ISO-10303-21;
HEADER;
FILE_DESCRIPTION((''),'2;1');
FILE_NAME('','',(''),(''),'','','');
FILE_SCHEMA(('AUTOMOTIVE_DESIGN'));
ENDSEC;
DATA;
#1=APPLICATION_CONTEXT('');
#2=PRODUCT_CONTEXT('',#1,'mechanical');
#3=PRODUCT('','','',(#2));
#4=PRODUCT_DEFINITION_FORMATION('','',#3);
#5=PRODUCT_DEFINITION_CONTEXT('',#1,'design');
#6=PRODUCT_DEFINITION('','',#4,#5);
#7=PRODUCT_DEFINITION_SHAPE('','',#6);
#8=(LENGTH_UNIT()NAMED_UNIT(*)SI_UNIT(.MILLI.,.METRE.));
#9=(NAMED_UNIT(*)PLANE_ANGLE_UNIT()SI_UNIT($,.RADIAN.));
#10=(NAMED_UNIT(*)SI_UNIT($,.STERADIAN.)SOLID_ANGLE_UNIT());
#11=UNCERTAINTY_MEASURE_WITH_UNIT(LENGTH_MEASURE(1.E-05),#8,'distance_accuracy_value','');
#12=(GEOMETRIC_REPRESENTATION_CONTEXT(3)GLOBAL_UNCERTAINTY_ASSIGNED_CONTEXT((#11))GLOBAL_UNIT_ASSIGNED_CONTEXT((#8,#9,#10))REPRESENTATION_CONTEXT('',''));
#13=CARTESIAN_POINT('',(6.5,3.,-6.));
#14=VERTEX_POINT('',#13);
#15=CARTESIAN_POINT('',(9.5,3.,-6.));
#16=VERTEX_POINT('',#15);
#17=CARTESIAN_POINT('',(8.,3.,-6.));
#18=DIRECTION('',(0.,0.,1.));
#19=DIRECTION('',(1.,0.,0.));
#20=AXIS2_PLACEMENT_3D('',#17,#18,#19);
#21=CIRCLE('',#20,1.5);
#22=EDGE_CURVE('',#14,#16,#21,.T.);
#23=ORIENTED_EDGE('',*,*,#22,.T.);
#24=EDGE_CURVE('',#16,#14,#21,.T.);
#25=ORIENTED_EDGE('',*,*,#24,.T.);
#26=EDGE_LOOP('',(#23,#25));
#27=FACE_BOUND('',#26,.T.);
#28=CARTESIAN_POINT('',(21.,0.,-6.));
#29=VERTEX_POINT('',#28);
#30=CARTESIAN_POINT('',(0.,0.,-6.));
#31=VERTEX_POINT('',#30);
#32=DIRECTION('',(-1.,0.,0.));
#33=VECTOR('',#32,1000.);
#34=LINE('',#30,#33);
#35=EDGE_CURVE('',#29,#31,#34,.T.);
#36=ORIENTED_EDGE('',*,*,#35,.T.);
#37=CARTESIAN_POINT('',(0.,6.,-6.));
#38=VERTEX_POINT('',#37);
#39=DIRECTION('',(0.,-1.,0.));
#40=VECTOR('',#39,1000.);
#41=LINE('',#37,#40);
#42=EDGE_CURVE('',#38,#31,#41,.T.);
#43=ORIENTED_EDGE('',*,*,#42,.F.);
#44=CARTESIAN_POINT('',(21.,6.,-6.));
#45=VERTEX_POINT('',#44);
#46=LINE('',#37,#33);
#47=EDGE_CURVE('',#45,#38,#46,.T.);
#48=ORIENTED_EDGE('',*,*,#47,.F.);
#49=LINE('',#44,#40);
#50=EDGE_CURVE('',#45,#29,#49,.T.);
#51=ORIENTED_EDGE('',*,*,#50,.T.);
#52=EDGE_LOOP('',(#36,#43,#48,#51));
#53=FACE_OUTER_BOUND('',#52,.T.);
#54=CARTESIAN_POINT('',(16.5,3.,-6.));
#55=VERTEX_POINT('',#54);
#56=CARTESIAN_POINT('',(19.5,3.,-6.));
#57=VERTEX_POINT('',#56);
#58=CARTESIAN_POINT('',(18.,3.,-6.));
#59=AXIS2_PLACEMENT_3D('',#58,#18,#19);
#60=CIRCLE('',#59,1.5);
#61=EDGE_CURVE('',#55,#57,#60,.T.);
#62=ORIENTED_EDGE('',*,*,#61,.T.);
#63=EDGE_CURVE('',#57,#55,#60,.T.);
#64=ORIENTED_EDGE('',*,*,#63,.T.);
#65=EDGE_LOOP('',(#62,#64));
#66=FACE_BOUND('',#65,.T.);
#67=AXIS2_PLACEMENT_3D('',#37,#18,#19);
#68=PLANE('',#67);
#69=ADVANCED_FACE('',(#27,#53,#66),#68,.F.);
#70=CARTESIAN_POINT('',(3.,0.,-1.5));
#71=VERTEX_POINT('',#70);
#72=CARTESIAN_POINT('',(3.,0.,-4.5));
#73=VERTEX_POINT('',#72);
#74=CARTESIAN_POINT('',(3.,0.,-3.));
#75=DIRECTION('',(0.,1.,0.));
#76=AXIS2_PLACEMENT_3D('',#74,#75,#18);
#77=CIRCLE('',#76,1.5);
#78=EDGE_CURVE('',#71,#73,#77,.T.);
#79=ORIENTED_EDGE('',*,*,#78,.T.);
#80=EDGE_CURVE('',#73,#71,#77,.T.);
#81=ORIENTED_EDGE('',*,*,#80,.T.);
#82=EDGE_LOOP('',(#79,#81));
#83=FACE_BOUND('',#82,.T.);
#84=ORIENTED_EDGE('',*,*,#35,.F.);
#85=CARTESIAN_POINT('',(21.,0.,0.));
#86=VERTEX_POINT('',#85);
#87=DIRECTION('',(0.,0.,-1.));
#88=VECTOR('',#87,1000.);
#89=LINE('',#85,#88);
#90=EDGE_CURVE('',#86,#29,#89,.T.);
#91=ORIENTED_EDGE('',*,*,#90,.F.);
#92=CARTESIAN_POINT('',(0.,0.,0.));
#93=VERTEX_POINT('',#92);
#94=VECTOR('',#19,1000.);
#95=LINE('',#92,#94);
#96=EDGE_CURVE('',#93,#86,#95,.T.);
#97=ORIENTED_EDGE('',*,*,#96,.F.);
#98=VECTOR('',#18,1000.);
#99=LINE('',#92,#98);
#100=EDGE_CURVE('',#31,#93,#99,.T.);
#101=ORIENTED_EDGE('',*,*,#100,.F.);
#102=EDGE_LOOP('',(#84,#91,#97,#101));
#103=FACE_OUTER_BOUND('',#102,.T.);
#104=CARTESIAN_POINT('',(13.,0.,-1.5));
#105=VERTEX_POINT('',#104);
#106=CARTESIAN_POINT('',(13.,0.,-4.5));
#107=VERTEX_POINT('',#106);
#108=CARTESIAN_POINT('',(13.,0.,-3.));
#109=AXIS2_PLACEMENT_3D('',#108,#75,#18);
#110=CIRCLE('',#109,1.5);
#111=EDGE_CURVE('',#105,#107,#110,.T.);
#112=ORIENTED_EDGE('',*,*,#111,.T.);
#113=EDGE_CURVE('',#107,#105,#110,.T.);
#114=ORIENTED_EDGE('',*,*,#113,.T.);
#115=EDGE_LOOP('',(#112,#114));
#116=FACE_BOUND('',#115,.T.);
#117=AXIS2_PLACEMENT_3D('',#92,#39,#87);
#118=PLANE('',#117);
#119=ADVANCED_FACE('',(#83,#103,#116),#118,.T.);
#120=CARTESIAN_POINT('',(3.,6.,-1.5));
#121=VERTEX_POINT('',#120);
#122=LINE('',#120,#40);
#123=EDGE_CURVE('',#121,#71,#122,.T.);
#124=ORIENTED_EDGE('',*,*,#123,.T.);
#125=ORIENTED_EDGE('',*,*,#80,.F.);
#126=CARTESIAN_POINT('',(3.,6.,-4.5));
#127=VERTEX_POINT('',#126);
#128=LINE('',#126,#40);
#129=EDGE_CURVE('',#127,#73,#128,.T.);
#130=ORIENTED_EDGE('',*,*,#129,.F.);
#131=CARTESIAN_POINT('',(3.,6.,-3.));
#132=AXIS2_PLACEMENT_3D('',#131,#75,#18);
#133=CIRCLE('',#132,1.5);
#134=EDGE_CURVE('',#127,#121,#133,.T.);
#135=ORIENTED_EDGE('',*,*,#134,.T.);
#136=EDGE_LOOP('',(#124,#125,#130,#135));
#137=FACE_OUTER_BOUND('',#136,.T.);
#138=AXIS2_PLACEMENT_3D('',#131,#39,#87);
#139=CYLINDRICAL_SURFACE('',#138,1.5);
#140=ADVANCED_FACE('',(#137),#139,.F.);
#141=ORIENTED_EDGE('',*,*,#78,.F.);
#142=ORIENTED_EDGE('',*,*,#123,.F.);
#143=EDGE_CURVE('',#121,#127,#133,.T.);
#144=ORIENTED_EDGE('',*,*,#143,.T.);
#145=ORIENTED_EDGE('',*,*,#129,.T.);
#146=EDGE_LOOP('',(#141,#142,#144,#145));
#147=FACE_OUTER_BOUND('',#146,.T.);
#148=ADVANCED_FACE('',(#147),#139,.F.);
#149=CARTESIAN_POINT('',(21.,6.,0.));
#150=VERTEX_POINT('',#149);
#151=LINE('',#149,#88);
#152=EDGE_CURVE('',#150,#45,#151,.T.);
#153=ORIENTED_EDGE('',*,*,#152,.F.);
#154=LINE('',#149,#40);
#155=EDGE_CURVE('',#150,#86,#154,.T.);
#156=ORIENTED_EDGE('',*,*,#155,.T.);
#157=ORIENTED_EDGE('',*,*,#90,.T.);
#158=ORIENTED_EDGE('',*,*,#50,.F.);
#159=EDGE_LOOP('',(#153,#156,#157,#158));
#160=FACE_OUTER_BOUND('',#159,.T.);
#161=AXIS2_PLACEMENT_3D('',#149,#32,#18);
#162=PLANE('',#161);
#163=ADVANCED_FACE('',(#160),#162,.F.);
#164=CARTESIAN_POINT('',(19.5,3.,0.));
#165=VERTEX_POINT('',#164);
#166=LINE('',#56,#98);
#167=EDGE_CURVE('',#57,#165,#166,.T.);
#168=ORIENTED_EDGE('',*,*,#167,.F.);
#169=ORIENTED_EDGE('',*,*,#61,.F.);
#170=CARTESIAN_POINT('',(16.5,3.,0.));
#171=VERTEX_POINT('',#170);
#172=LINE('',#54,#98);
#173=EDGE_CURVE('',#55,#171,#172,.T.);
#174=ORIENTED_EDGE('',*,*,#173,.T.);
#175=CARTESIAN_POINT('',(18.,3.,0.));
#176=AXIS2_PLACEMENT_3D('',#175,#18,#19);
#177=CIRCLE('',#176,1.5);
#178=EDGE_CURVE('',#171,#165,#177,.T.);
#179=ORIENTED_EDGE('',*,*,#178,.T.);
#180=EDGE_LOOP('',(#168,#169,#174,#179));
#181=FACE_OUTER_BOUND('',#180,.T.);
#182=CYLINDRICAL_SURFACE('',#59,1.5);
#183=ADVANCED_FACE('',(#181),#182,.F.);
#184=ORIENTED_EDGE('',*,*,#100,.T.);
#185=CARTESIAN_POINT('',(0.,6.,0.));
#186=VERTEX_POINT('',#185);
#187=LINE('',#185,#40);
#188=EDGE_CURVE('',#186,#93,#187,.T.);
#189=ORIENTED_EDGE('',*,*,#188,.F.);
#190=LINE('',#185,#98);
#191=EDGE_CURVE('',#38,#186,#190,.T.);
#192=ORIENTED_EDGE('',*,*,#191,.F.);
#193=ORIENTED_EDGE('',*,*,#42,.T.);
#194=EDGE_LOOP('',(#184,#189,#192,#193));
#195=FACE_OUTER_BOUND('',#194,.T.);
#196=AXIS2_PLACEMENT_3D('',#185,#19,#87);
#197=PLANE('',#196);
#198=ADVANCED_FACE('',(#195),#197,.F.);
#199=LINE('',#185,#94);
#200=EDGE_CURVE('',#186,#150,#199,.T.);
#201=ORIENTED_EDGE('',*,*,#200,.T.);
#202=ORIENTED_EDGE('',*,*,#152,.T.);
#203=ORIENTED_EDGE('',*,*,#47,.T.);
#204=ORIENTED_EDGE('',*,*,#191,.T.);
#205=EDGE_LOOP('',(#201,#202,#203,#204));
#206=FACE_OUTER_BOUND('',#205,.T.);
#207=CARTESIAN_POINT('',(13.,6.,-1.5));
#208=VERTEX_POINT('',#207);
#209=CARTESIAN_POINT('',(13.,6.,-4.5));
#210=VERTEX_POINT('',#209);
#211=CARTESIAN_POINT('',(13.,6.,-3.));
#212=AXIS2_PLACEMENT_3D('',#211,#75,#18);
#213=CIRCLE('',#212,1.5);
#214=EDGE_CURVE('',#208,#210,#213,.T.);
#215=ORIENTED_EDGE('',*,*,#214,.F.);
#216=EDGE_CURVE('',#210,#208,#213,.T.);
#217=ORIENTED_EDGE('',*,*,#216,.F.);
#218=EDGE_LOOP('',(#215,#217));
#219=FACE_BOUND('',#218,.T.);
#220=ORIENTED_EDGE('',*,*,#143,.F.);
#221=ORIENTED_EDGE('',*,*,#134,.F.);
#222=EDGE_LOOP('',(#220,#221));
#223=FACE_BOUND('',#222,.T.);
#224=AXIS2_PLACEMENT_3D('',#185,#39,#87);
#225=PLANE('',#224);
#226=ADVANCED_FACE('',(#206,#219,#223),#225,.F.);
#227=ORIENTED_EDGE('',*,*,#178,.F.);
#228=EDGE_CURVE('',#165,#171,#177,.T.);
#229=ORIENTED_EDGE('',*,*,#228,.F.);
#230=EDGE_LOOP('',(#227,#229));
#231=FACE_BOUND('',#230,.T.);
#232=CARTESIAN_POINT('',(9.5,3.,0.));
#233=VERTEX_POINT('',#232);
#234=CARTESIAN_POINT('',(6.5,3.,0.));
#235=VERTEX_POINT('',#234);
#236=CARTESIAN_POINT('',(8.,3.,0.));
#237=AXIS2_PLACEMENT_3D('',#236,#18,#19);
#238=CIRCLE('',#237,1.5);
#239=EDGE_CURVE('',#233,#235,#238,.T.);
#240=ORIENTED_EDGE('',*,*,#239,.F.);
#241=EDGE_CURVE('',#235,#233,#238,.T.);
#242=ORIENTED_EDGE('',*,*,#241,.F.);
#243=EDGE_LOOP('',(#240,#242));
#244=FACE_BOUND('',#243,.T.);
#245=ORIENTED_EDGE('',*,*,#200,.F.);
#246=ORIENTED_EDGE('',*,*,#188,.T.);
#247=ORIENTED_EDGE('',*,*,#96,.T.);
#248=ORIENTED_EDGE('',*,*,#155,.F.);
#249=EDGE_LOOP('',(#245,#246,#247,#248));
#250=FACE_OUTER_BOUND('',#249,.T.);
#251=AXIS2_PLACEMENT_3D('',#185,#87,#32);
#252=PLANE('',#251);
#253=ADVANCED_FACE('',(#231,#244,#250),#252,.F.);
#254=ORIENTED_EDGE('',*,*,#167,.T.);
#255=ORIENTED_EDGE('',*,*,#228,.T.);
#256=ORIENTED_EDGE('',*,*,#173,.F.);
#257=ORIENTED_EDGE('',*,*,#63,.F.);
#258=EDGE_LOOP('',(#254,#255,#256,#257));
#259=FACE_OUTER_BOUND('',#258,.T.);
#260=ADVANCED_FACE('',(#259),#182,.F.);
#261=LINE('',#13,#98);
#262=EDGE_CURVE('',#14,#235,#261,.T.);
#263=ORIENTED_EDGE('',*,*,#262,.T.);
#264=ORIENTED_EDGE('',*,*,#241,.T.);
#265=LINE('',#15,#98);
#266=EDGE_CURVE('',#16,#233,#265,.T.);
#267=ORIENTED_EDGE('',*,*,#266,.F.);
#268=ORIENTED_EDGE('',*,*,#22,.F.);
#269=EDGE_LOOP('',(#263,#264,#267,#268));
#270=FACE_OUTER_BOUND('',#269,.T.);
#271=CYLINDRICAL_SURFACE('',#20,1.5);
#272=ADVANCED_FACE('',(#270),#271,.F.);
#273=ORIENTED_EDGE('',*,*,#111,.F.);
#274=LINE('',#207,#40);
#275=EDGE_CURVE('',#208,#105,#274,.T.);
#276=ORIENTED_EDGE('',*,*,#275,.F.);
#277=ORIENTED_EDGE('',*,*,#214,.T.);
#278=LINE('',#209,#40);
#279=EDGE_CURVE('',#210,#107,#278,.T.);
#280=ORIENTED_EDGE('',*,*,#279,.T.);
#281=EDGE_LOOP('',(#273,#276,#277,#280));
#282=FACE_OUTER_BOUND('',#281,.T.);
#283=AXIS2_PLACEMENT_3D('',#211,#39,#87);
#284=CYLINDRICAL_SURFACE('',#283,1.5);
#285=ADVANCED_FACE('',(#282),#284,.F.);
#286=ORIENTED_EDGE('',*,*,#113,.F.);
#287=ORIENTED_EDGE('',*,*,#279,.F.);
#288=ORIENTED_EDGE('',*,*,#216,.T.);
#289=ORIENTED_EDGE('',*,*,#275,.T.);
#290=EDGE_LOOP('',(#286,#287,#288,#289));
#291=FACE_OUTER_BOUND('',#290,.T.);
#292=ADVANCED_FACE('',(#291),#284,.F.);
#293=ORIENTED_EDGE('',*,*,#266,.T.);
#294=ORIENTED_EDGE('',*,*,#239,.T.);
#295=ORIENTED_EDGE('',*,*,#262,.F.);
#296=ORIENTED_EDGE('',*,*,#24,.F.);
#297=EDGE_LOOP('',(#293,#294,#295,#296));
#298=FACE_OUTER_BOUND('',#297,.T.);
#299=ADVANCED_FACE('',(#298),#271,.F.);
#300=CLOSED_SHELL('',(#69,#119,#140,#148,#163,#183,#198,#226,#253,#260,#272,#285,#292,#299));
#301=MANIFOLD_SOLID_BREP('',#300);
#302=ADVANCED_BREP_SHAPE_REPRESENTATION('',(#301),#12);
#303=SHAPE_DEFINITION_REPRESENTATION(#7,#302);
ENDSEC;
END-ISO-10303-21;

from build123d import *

# Parameters (mm, degrees)
SKETCH_1_W          = 21
SKETCH_1_H          = 6
SKETCH_1_R          = 1.5
EXTRUDE_1_DEPTH     = 6
SKETCH_2_R          = 1.5
CUT_EXTRUDE_1_DEPTH = 23.649503306


with BuildPart() as part:
    # 草图1 → 凸台-拉伸1 (new body)
    with BuildSketch(Plane(origin=(0, 0, 0), x_dir=(1, 0, 0), z_dir=(0, 1, 0))):
        with Locations((10.5, 3)):
            Rectangle(SKETCH_1_W, SKETCH_1_H)
        with Locations(Location((3, 3, 0), (0, 0, 270))):
            Circle(SKETCH_1_R, mode=Mode.SUBTRACT)
        with Locations(Location((13, 3, 0), (0, 0, 270))):
            Circle(SKETCH_1_R, mode=Mode.SUBTRACT)
    extrude(amount=EXTRUDE_1_DEPTH)

    # 草图2 → 切除-拉伸1 (cut, through all)
    with BuildSketch(Plane.XY):
        with Locations((18, 3)):
            Circle(SKETCH_2_R)
        with Locations((8, 3)):
            Circle(SKETCH_2_R)
    extrude(amount=-CUT_EXTRUDE_1_DEPTH, mode=Mode.SUBTRACT)


solid = part.part
